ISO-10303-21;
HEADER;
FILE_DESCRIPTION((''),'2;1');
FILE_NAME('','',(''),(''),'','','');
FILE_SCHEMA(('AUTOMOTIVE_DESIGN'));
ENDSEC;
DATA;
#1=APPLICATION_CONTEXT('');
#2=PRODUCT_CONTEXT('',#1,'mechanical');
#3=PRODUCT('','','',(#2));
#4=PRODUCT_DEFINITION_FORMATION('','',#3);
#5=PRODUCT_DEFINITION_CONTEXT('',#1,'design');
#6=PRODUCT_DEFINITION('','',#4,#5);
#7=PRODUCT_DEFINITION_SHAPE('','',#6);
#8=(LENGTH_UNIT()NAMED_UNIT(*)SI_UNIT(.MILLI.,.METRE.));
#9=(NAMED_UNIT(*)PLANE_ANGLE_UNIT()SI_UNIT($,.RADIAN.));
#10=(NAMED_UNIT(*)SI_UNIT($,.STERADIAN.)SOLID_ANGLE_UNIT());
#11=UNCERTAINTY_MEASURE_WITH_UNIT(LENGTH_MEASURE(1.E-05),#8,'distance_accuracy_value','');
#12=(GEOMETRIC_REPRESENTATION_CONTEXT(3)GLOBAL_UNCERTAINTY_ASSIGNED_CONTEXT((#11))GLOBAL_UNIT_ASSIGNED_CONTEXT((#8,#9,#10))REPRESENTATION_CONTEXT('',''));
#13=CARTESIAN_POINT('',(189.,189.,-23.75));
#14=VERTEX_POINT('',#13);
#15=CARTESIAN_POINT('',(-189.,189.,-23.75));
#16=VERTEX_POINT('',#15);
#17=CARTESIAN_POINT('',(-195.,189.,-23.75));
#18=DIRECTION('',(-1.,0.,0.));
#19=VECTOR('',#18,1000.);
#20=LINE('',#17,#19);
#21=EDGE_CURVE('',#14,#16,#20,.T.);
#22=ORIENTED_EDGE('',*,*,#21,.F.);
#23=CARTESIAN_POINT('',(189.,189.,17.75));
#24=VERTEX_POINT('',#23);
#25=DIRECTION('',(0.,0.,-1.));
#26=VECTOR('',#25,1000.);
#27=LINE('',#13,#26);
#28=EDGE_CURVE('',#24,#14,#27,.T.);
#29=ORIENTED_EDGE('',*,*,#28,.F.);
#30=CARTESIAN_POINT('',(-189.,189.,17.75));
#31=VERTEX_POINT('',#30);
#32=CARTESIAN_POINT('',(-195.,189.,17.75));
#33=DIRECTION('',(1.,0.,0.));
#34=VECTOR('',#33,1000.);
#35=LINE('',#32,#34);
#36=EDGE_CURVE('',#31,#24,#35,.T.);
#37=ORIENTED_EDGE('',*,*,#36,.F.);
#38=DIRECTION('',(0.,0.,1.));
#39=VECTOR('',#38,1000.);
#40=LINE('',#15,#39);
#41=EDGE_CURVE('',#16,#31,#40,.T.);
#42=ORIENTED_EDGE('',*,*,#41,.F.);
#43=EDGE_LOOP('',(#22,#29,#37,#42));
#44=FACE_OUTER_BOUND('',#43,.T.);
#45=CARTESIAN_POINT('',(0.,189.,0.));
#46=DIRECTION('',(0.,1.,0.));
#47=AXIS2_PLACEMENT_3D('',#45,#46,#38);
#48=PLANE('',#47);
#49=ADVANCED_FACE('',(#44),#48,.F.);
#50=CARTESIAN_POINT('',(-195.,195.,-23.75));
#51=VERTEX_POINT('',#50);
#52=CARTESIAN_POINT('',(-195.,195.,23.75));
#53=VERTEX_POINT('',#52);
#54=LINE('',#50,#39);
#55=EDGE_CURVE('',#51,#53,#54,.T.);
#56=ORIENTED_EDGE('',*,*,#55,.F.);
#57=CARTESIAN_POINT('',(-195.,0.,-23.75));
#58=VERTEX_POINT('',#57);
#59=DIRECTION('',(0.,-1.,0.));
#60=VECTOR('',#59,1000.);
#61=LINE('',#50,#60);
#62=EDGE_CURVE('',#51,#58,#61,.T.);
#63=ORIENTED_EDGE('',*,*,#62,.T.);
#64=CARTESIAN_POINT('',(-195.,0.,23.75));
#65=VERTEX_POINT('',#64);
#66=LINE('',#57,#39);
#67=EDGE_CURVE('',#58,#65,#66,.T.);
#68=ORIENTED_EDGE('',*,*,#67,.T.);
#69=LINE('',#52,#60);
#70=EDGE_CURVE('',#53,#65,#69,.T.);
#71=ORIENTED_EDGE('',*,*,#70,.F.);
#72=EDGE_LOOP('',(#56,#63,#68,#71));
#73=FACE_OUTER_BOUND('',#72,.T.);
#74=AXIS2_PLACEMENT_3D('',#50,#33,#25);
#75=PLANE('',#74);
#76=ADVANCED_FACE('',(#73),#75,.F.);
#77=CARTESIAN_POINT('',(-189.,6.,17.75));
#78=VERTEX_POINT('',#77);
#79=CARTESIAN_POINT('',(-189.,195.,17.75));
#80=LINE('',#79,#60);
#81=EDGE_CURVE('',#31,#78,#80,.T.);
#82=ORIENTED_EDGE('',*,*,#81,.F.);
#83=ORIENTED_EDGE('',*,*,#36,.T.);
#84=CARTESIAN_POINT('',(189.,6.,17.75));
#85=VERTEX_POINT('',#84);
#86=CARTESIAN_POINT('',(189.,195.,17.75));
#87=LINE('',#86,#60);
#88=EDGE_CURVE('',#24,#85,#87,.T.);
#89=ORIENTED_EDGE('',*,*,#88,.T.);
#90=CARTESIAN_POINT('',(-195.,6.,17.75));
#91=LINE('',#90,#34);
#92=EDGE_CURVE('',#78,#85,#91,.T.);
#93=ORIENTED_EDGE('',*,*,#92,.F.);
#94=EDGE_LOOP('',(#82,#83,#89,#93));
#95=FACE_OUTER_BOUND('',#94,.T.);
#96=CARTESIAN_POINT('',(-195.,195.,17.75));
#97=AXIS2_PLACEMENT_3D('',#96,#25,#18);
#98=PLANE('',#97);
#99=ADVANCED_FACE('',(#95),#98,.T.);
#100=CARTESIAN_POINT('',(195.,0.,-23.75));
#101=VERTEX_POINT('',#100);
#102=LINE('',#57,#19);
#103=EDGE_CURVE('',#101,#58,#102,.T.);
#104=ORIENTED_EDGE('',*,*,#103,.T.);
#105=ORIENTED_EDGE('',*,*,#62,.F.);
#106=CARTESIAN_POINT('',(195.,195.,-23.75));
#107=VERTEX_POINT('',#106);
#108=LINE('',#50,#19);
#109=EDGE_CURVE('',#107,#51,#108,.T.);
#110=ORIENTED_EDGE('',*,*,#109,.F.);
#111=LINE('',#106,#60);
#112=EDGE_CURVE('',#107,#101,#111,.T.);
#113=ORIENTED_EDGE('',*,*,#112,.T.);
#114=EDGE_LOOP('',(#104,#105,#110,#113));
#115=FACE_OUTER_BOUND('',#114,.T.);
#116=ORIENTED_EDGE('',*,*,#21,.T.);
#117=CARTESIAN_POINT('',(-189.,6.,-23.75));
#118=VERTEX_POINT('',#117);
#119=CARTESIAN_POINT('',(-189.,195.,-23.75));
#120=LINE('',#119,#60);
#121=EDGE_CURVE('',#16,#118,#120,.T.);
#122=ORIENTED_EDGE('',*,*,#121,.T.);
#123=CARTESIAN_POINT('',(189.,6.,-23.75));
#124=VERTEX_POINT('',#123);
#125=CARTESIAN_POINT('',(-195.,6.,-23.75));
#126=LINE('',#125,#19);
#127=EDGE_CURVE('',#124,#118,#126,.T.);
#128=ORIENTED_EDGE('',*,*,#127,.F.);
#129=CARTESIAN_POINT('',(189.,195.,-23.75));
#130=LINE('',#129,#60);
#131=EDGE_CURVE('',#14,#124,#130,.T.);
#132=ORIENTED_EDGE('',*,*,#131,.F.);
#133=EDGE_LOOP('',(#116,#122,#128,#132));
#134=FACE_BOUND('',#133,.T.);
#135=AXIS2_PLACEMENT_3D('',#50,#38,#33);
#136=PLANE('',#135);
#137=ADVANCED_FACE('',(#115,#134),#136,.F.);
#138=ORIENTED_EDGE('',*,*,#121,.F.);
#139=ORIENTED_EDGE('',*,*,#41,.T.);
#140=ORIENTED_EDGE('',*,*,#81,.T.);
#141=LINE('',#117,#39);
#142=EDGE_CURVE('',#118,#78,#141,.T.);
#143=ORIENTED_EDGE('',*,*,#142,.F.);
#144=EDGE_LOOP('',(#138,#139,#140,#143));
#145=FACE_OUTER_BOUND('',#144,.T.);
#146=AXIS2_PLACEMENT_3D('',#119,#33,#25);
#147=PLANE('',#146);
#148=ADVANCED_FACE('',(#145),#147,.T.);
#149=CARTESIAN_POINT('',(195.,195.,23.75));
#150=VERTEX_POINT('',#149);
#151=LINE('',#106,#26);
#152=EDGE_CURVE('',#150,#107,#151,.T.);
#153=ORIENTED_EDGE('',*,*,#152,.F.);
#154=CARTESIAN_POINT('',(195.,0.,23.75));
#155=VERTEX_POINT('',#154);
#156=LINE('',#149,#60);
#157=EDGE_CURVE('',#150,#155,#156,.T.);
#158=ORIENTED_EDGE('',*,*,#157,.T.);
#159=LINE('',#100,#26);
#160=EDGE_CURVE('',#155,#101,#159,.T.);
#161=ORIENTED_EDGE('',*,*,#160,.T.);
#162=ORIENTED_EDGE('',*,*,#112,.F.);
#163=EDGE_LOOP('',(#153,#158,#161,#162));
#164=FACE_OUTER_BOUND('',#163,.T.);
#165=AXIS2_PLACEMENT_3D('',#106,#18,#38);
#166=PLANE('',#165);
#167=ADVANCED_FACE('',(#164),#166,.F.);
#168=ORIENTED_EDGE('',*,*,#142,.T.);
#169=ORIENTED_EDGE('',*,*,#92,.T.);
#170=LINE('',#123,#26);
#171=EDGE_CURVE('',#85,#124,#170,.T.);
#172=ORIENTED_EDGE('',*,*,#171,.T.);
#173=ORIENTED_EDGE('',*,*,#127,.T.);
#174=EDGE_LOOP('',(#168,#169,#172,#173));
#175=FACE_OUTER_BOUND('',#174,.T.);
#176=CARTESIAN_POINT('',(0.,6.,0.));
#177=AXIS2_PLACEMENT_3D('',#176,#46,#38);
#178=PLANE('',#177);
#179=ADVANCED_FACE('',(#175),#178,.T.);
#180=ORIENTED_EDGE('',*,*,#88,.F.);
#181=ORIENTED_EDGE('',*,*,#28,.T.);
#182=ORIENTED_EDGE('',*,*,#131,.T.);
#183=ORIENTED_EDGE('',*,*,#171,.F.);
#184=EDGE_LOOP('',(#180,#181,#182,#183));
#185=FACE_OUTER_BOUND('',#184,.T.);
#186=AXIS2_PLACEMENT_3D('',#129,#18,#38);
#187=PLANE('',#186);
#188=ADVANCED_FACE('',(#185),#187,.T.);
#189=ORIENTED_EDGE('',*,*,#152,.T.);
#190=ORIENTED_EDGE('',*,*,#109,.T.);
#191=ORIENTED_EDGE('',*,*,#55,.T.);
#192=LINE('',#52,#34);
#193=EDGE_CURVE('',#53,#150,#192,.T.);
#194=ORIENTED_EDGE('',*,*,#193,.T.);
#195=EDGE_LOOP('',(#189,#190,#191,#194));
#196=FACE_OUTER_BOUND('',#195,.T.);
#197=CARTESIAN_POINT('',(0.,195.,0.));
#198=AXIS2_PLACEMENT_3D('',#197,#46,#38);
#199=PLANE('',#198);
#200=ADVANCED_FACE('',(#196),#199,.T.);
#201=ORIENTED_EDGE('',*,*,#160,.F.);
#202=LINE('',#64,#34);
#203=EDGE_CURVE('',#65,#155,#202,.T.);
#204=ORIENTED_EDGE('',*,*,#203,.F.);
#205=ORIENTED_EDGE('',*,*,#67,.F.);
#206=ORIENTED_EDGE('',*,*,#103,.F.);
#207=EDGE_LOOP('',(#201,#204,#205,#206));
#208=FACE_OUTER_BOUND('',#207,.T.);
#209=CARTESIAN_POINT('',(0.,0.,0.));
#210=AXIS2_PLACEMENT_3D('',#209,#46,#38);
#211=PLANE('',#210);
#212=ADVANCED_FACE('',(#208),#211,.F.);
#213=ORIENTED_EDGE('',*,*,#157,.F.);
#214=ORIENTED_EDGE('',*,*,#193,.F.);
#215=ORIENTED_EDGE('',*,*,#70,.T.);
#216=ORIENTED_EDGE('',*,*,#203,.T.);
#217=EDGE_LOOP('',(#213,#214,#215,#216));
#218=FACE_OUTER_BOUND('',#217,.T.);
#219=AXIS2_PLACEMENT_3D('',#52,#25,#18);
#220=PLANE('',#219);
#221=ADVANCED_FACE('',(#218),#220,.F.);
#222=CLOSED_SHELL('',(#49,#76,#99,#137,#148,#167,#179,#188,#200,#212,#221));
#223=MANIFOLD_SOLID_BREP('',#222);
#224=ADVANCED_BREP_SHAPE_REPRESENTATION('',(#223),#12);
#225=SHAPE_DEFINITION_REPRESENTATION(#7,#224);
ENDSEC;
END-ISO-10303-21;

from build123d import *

# Parameters (mm, degrees)
SKETCH1_W           = 390
SKETCH1_H           = 47.5
BOSS_EXTRUDE1_DEPTH = 195
SHELL1_T            = -6


with BuildPart() as part:
    # Sketch1 → Boss-Extrude1 (new body)
    with BuildSketch(Plane(origin=(0, 0, 0), x_dir=(1, 0, 0), z_dir=(0, 1, 0))):
        Rectangle(SKETCH1_W, SKETCH1_H)
    extrude(amount=BOSS_EXTRUDE1_DEPTH)

    # Shell1
    shell1_openings = [part.faces().sort_by_distance(p)[0] for p in [
        (0, 97.5, -23.75),
    ]]
    offset(amount=SHELL1_T, openings=shell1_openings, kind=Kind.INTERSECTION)


solid = part.part
